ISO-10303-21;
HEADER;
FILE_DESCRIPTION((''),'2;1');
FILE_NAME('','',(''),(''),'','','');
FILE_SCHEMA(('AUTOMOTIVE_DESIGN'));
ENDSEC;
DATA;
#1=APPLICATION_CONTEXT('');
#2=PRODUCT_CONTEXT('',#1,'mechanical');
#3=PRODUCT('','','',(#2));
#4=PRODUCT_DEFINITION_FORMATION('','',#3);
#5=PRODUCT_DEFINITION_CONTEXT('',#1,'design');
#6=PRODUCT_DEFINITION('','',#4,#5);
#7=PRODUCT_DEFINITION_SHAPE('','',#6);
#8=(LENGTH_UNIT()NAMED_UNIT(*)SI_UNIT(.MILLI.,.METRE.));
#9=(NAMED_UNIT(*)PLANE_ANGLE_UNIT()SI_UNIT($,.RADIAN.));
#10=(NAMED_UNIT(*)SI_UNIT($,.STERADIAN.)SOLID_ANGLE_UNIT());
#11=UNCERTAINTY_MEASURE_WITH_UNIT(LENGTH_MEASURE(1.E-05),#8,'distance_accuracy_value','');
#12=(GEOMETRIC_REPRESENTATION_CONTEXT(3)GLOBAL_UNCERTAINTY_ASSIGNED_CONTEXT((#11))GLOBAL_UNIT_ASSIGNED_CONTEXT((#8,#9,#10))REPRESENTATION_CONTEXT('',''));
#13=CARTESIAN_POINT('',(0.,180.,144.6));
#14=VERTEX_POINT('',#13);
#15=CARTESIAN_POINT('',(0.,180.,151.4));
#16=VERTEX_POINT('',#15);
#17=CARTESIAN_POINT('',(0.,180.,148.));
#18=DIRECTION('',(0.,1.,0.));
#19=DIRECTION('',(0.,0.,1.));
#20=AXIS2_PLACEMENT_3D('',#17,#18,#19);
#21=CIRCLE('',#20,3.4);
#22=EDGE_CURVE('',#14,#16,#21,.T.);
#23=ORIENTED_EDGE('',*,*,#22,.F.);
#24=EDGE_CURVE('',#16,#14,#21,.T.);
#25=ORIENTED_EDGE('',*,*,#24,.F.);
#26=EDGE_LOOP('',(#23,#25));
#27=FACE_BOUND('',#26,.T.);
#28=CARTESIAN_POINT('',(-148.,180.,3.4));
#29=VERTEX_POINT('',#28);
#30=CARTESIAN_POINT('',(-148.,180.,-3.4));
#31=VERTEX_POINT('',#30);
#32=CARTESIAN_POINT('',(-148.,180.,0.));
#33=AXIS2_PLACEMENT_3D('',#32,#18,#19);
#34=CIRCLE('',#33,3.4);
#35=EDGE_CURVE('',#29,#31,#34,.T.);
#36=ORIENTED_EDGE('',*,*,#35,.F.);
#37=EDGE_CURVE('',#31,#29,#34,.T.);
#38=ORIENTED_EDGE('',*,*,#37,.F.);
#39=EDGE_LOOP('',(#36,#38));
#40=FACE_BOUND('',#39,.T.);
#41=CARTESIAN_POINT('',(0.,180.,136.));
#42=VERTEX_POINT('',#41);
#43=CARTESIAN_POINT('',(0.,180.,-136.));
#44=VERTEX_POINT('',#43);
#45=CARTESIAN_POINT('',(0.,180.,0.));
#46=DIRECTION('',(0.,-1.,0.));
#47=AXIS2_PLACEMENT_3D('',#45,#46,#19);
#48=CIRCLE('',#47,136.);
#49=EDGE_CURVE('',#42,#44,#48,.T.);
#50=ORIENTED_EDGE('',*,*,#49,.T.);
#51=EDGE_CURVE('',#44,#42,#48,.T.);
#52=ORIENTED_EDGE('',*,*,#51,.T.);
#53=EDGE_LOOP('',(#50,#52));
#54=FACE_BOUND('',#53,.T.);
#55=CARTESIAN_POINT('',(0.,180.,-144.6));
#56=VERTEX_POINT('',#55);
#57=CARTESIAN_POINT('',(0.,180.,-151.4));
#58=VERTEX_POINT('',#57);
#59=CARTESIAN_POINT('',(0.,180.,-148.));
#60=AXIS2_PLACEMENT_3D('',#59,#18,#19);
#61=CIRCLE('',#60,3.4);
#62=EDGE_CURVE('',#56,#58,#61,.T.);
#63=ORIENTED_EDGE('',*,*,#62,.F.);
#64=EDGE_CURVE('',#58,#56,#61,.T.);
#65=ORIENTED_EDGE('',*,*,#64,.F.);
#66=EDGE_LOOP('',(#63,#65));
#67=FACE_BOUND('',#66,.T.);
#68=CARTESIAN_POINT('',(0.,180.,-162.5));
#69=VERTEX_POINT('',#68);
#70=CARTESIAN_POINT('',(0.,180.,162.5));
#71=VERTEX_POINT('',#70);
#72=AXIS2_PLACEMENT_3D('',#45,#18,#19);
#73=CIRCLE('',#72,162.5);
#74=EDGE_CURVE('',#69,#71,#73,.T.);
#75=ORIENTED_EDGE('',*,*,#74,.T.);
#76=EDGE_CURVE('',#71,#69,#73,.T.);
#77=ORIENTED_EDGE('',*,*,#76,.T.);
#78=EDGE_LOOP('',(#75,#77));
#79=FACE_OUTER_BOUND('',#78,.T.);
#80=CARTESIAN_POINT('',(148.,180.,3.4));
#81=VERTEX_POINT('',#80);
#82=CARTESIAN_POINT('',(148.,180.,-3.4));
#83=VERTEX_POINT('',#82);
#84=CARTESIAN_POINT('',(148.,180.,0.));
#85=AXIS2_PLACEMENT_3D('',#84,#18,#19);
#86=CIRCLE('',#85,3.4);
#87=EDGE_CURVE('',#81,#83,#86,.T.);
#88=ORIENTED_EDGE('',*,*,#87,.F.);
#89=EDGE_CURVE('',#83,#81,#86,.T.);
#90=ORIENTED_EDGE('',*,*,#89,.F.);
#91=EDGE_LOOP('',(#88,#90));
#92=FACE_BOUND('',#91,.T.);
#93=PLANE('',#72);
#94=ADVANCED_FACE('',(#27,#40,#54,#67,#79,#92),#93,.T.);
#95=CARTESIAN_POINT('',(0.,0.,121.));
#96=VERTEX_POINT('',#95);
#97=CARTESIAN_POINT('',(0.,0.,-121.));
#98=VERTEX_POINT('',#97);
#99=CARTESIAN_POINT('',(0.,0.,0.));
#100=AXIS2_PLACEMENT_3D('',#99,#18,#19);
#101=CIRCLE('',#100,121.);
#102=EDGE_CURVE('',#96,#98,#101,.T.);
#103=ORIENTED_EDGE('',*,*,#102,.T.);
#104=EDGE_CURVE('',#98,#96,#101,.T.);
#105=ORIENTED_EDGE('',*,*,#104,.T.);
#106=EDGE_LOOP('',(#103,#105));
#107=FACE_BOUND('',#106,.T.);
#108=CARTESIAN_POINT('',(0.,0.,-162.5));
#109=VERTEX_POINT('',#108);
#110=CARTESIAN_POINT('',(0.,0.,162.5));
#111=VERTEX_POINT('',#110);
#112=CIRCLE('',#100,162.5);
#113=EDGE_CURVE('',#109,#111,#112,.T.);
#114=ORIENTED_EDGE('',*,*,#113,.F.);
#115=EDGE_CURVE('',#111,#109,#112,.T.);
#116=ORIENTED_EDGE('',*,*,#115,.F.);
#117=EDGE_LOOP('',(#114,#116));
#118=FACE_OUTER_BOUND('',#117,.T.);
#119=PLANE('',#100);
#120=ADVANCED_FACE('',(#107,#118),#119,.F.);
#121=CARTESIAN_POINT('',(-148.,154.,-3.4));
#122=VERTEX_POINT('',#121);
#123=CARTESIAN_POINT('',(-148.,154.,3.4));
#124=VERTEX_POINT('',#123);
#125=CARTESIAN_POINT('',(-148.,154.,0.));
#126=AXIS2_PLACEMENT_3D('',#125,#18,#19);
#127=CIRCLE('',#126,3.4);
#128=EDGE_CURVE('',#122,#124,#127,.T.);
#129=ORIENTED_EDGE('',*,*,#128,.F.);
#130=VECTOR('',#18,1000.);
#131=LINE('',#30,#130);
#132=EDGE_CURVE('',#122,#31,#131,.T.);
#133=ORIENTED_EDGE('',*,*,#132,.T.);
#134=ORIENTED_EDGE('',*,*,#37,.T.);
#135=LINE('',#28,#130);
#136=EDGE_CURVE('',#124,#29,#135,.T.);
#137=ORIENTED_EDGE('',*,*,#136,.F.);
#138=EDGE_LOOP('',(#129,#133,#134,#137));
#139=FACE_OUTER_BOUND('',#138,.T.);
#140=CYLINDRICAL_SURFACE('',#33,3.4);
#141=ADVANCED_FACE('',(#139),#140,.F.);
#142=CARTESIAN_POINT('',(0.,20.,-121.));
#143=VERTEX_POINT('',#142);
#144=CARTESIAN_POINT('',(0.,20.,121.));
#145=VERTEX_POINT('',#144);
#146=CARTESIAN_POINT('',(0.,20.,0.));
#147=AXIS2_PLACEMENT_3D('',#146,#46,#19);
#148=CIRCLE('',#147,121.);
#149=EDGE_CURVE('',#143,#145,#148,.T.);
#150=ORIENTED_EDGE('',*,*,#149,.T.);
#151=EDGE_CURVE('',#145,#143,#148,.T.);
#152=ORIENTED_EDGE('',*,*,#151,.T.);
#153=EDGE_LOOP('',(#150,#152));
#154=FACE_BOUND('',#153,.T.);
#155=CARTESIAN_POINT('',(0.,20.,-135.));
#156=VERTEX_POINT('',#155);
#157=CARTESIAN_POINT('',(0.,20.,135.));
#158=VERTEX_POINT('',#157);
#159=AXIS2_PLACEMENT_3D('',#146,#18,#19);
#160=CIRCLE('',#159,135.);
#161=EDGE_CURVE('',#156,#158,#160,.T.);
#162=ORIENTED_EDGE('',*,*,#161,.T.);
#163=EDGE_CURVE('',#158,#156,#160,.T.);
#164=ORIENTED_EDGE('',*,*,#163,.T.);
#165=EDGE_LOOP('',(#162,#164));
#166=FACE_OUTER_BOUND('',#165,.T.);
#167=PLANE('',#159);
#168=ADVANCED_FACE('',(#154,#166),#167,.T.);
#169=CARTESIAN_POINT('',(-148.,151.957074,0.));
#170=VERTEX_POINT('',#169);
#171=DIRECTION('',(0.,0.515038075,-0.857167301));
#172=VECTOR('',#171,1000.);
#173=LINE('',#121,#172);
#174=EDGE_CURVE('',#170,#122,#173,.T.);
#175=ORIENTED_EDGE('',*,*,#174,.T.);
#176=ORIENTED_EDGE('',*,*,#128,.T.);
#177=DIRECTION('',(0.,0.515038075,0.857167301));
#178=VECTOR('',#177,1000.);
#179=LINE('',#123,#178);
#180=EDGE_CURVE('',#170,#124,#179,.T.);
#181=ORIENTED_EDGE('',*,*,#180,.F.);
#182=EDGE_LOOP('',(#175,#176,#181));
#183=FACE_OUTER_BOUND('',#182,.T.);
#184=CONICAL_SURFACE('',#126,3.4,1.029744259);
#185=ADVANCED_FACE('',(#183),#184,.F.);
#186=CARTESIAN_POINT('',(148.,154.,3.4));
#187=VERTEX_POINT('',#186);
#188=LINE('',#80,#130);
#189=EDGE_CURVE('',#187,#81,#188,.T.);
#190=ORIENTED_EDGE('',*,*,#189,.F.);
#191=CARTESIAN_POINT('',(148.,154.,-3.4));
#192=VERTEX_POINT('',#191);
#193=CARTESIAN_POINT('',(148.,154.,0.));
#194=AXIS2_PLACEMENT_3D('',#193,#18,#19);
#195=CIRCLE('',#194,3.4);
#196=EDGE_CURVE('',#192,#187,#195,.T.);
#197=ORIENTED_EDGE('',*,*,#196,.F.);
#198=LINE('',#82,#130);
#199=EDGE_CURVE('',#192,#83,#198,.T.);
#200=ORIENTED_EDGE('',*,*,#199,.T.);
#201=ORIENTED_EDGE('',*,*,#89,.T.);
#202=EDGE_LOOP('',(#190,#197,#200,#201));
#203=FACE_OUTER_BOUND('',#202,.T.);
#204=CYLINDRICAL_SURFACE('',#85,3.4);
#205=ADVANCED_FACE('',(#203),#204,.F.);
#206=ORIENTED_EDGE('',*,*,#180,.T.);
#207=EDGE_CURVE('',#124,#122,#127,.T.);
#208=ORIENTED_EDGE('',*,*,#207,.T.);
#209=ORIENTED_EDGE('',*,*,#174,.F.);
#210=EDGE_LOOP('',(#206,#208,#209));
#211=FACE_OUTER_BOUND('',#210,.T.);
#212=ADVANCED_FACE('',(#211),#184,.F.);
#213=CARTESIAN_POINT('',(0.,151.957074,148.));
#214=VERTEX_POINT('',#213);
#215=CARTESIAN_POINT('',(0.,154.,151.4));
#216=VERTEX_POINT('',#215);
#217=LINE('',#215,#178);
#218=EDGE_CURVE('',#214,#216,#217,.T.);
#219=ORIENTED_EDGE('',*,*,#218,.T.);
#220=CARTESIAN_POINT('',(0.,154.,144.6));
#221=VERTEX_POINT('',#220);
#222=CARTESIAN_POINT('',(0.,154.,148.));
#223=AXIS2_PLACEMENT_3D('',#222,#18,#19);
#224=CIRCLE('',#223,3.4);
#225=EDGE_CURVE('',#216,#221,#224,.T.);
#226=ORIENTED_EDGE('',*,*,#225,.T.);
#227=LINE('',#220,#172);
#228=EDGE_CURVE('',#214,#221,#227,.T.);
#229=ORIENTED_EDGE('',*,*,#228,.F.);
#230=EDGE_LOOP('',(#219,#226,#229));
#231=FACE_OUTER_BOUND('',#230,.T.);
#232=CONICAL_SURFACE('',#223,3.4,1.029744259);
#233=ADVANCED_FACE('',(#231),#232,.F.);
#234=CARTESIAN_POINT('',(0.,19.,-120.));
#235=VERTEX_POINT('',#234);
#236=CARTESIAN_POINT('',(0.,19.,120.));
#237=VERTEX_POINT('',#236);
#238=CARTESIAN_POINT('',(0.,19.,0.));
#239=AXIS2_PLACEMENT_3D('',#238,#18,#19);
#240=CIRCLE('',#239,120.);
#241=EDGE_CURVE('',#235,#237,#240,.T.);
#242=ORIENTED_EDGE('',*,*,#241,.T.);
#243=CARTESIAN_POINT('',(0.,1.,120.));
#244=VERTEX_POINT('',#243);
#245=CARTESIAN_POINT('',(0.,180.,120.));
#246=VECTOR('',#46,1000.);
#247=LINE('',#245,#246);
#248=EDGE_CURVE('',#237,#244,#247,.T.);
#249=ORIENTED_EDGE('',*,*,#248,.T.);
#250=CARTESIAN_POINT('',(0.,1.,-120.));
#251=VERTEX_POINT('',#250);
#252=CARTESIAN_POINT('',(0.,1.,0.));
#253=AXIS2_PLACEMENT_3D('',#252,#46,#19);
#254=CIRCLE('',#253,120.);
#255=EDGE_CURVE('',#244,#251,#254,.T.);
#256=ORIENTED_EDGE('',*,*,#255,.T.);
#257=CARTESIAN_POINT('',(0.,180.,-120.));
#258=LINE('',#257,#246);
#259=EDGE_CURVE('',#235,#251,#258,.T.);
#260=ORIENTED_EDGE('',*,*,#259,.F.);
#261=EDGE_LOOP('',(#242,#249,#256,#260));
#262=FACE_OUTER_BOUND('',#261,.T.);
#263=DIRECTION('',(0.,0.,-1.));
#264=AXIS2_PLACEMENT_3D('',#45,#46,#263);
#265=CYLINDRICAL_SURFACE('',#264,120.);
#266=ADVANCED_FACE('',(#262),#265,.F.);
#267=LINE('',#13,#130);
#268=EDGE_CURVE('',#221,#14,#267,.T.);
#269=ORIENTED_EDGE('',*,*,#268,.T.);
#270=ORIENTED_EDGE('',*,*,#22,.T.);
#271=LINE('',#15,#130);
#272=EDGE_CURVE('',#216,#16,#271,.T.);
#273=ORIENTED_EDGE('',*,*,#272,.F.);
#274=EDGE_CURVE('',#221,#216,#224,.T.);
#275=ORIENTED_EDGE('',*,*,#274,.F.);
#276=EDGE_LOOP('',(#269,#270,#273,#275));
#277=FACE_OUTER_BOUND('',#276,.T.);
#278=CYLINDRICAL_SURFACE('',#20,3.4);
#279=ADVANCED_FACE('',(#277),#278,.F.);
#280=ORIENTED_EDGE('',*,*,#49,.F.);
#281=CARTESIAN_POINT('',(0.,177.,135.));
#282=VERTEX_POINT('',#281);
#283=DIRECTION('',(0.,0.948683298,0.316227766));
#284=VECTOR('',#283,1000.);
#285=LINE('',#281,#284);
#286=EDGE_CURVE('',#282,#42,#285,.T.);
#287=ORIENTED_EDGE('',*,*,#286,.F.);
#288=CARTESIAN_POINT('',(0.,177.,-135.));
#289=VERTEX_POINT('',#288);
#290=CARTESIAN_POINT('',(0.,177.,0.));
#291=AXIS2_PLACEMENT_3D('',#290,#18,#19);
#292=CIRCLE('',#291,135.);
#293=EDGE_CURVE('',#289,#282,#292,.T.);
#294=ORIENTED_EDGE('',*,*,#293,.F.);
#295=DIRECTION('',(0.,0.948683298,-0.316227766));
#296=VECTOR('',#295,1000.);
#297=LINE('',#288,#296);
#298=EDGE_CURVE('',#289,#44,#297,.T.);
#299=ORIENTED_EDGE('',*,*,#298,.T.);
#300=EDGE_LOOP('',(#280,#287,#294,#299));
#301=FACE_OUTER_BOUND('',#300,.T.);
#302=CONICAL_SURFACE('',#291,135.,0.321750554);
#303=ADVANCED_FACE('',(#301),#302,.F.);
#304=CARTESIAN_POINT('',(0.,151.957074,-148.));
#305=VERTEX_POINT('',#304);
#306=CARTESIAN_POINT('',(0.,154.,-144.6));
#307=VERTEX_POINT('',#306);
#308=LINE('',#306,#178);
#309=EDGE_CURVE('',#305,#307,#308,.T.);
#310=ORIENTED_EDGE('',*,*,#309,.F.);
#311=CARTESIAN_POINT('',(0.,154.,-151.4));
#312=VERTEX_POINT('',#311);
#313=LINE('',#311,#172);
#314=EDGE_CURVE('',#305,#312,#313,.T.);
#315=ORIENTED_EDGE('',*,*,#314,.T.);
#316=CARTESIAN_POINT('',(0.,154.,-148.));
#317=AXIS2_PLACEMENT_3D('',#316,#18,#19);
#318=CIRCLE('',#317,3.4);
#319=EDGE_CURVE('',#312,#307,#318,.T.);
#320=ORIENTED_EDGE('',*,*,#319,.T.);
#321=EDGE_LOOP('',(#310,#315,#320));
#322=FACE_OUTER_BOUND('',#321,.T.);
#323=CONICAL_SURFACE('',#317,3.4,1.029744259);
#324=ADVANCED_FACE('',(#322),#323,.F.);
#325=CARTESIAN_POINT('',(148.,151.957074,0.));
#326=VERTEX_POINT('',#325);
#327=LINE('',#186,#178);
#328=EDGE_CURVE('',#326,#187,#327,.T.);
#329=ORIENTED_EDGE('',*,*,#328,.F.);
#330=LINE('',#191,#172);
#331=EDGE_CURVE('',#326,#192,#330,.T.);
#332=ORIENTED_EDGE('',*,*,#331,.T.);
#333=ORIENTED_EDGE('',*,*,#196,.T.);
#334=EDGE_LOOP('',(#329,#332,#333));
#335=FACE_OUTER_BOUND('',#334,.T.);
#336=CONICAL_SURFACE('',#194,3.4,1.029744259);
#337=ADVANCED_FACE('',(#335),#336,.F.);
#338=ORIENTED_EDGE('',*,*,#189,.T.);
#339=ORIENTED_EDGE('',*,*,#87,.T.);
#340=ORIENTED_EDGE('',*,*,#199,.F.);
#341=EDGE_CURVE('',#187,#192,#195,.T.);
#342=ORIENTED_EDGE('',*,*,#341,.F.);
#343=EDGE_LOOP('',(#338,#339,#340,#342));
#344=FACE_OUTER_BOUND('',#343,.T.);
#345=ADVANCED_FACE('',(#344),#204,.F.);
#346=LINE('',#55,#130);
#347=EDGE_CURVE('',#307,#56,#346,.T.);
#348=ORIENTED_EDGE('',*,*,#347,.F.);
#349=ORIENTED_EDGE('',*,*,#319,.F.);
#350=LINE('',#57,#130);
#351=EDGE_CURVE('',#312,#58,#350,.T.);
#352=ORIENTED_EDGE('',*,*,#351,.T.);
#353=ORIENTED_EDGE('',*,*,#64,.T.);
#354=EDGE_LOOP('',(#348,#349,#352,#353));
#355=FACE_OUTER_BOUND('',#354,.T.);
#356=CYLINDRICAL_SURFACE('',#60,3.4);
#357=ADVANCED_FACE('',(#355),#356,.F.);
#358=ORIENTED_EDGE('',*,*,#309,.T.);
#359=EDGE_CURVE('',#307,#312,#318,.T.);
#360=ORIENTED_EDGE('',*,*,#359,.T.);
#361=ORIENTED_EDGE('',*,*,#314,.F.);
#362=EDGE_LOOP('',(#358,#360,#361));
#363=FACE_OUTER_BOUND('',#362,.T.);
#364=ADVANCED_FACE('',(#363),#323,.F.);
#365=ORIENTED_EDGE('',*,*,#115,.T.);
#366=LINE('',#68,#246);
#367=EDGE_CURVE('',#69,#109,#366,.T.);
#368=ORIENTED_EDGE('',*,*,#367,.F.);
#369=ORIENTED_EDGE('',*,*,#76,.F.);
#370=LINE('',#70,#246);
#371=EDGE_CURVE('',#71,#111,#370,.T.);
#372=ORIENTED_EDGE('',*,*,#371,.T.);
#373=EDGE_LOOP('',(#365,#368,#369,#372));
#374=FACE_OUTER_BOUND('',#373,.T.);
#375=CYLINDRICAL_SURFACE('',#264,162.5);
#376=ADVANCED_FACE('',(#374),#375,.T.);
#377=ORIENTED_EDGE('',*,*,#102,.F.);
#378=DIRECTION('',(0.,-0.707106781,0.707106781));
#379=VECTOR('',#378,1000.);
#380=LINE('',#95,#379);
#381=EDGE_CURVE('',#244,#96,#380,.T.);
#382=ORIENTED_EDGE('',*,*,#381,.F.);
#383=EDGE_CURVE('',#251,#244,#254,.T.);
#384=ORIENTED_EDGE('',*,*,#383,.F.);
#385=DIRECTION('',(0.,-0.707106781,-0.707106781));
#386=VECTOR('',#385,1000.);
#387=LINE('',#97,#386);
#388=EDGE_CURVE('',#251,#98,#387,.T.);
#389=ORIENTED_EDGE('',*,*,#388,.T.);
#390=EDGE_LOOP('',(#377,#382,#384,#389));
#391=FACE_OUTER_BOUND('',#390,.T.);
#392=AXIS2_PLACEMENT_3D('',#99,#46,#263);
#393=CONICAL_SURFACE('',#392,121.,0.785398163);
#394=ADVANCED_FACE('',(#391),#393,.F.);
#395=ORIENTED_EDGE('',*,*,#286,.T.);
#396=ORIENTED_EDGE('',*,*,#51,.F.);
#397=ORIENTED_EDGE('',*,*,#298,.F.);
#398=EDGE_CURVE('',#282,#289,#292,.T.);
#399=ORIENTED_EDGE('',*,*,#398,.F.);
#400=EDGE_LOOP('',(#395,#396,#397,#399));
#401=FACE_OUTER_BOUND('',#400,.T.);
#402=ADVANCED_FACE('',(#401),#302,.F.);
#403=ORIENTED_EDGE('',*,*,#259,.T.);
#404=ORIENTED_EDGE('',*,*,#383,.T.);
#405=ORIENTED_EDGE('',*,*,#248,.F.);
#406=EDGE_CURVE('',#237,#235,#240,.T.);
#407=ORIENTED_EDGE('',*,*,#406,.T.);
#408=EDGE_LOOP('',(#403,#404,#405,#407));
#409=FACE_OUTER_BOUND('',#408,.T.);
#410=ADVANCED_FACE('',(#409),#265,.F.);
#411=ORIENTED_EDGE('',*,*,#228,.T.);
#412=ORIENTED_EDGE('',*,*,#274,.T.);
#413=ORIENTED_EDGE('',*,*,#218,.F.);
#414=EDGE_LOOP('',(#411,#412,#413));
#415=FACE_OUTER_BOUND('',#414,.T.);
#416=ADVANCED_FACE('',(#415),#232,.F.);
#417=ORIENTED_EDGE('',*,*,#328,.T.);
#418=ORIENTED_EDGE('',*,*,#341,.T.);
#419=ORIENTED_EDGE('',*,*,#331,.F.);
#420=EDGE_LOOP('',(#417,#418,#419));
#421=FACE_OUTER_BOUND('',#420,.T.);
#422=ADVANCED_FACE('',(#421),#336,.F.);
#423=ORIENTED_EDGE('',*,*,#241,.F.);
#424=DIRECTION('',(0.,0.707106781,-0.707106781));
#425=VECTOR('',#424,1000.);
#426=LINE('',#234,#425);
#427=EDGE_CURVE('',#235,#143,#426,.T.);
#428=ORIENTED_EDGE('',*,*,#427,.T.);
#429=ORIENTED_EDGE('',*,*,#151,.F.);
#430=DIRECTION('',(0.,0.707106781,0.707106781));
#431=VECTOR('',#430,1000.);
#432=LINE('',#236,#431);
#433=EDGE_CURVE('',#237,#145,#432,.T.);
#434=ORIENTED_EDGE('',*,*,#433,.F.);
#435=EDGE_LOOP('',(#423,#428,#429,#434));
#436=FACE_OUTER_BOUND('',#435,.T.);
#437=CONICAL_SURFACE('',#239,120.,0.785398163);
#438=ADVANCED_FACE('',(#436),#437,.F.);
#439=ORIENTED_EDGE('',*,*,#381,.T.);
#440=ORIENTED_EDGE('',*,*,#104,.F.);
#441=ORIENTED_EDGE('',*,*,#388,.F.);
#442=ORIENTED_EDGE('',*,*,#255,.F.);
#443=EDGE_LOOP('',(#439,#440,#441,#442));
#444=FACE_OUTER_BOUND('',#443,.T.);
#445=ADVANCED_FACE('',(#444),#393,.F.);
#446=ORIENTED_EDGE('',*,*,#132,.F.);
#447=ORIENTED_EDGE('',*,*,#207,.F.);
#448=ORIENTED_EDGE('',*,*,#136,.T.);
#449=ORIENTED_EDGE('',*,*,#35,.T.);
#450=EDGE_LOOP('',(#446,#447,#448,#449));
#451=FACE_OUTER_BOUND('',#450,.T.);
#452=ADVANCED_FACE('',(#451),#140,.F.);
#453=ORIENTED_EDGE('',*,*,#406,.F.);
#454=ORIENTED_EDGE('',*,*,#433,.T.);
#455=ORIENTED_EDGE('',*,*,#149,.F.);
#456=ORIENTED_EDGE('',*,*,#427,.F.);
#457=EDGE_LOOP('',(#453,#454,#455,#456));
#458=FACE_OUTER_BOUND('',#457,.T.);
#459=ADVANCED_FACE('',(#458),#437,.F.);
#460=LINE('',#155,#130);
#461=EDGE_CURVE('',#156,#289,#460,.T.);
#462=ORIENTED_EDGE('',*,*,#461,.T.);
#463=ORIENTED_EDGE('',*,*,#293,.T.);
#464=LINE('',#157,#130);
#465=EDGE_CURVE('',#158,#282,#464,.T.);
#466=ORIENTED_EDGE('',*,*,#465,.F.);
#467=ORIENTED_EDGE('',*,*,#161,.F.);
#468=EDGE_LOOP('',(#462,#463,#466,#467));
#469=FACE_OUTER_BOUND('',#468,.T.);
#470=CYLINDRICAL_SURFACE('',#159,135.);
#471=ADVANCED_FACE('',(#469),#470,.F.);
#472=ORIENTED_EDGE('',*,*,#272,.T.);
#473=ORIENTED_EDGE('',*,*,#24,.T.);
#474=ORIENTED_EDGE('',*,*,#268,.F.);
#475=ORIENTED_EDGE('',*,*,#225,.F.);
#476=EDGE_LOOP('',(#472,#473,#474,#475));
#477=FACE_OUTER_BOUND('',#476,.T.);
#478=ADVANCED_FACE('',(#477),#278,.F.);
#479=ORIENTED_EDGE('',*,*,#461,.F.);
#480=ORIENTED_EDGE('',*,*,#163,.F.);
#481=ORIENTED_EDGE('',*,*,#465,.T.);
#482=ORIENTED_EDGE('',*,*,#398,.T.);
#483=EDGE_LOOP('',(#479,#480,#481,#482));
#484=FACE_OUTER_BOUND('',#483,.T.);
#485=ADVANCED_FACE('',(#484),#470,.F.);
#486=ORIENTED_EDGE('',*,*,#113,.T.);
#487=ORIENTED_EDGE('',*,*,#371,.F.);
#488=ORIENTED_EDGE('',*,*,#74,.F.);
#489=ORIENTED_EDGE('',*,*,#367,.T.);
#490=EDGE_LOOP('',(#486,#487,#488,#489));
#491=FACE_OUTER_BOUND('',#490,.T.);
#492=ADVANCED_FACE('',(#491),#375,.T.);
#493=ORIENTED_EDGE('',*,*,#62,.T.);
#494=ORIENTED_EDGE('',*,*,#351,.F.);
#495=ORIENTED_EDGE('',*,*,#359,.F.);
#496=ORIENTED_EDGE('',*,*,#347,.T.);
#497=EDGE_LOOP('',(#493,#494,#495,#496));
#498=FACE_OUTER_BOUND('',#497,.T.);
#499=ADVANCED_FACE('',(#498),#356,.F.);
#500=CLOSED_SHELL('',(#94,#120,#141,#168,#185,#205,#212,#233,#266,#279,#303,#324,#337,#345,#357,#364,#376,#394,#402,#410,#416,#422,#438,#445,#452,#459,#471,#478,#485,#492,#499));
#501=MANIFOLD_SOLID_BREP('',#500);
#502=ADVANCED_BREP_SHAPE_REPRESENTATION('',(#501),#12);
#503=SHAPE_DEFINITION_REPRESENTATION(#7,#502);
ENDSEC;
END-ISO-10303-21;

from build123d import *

# Parameters (mm, degrees)
SKETCH1_R             = 162.5
SKETCH1_R_2           = 120
BOSS_EXTRUDE1_DEPTH   = 180
SKETCH2_R             = 135
CUT_EXTRUDE1_DEPTH    = 160
CHAMFER1_SIZE         = 1
CHAMFER1_SIZE2        = 3
CHAMFER2_SIZE         = 1
M8_TAPPED_HOLE1_D     = 6.8
M8_TAPPED_HOLE1_DEPTH = 26
M8_TAPPED_HOLE1_TIP   = 2.042926105


with BuildPart() as part:
    # Sketch1 → Boss-Extrude1 (new body)
    with BuildSketch(Plane(origin=(0, 0, 0), x_dir=(1, 0, 0), z_dir=(0, 1, 0))):
        with Locations(Location((0, 0, 0), (0, 0, 90))):
            Circle(SKETCH1_R)
        with Locations(Location((0, 0, 0), (0, 0, 90))):
            Circle(SKETCH1_R_2, mode=Mode.SUBTRACT)
    extrude(amount=BOSS_EXTRUDE1_DEPTH)

    # Sketch2 → Cut-Extrude1 (cut)
    with BuildSketch(Plane(origin=(0, 180, 0), x_dir=(1, 0, 0), z_dir=(0, 1, 0))):
        with Locations(Location((0, 0, 0), (0, 0, 270))):
            Circle(SKETCH2_R)
    extrude(amount=-CUT_EXTRUDE1_DEPTH, mode=Mode.SUBTRACT)

    # Chamfer1
    chamfer1_edges = [part.edges().sort_by_distance(p)[0] for p in [
        (0, 180, -135),
    ]]
    chamfer1_side = [part.faces().sort_by_distance(p)[0] for p in [
        (0, 180, 157.903805922),
    ]]
    chamfer(chamfer1_edges, length=CHAMFER1_SIZE, length2=CHAMFER1_SIZE2, reference=chamfer1_side[0])

    # Chamfer2
    chamfer2_edges = [part.edges().sort_by_distance(p)[0] for p in [
        (0, 20, 120),
        (0, 0, 120),
    ]]
    chamfer(chamfer2_edges, length=CHAMFER2_SIZE)

    # M8 Tapped Hole1
    with Locations(Plane(origin=(0, 180, 0), x_dir=(1, 0, 0), z_dir=(0, 1, 0))):
        with Locations((148, 0), (0, -148), (-148, 0), (0, 148)):
            Hole(M8_TAPPED_HOLE1_D / 2, depth=M8_TAPPED_HOLE1_DEPTH)
            with Locations((0, 0, -(M8_TAPPED_HOLE1_DEPTH + M8_TAPPED_HOLE1_TIP / 2))):  # 118° drill point
                Cone(0, M8_TAPPED_HOLE1_D / 2, M8_TAPPED_HOLE1_TIP, mode=Mode.SUBTRACT)


solid = part.part
